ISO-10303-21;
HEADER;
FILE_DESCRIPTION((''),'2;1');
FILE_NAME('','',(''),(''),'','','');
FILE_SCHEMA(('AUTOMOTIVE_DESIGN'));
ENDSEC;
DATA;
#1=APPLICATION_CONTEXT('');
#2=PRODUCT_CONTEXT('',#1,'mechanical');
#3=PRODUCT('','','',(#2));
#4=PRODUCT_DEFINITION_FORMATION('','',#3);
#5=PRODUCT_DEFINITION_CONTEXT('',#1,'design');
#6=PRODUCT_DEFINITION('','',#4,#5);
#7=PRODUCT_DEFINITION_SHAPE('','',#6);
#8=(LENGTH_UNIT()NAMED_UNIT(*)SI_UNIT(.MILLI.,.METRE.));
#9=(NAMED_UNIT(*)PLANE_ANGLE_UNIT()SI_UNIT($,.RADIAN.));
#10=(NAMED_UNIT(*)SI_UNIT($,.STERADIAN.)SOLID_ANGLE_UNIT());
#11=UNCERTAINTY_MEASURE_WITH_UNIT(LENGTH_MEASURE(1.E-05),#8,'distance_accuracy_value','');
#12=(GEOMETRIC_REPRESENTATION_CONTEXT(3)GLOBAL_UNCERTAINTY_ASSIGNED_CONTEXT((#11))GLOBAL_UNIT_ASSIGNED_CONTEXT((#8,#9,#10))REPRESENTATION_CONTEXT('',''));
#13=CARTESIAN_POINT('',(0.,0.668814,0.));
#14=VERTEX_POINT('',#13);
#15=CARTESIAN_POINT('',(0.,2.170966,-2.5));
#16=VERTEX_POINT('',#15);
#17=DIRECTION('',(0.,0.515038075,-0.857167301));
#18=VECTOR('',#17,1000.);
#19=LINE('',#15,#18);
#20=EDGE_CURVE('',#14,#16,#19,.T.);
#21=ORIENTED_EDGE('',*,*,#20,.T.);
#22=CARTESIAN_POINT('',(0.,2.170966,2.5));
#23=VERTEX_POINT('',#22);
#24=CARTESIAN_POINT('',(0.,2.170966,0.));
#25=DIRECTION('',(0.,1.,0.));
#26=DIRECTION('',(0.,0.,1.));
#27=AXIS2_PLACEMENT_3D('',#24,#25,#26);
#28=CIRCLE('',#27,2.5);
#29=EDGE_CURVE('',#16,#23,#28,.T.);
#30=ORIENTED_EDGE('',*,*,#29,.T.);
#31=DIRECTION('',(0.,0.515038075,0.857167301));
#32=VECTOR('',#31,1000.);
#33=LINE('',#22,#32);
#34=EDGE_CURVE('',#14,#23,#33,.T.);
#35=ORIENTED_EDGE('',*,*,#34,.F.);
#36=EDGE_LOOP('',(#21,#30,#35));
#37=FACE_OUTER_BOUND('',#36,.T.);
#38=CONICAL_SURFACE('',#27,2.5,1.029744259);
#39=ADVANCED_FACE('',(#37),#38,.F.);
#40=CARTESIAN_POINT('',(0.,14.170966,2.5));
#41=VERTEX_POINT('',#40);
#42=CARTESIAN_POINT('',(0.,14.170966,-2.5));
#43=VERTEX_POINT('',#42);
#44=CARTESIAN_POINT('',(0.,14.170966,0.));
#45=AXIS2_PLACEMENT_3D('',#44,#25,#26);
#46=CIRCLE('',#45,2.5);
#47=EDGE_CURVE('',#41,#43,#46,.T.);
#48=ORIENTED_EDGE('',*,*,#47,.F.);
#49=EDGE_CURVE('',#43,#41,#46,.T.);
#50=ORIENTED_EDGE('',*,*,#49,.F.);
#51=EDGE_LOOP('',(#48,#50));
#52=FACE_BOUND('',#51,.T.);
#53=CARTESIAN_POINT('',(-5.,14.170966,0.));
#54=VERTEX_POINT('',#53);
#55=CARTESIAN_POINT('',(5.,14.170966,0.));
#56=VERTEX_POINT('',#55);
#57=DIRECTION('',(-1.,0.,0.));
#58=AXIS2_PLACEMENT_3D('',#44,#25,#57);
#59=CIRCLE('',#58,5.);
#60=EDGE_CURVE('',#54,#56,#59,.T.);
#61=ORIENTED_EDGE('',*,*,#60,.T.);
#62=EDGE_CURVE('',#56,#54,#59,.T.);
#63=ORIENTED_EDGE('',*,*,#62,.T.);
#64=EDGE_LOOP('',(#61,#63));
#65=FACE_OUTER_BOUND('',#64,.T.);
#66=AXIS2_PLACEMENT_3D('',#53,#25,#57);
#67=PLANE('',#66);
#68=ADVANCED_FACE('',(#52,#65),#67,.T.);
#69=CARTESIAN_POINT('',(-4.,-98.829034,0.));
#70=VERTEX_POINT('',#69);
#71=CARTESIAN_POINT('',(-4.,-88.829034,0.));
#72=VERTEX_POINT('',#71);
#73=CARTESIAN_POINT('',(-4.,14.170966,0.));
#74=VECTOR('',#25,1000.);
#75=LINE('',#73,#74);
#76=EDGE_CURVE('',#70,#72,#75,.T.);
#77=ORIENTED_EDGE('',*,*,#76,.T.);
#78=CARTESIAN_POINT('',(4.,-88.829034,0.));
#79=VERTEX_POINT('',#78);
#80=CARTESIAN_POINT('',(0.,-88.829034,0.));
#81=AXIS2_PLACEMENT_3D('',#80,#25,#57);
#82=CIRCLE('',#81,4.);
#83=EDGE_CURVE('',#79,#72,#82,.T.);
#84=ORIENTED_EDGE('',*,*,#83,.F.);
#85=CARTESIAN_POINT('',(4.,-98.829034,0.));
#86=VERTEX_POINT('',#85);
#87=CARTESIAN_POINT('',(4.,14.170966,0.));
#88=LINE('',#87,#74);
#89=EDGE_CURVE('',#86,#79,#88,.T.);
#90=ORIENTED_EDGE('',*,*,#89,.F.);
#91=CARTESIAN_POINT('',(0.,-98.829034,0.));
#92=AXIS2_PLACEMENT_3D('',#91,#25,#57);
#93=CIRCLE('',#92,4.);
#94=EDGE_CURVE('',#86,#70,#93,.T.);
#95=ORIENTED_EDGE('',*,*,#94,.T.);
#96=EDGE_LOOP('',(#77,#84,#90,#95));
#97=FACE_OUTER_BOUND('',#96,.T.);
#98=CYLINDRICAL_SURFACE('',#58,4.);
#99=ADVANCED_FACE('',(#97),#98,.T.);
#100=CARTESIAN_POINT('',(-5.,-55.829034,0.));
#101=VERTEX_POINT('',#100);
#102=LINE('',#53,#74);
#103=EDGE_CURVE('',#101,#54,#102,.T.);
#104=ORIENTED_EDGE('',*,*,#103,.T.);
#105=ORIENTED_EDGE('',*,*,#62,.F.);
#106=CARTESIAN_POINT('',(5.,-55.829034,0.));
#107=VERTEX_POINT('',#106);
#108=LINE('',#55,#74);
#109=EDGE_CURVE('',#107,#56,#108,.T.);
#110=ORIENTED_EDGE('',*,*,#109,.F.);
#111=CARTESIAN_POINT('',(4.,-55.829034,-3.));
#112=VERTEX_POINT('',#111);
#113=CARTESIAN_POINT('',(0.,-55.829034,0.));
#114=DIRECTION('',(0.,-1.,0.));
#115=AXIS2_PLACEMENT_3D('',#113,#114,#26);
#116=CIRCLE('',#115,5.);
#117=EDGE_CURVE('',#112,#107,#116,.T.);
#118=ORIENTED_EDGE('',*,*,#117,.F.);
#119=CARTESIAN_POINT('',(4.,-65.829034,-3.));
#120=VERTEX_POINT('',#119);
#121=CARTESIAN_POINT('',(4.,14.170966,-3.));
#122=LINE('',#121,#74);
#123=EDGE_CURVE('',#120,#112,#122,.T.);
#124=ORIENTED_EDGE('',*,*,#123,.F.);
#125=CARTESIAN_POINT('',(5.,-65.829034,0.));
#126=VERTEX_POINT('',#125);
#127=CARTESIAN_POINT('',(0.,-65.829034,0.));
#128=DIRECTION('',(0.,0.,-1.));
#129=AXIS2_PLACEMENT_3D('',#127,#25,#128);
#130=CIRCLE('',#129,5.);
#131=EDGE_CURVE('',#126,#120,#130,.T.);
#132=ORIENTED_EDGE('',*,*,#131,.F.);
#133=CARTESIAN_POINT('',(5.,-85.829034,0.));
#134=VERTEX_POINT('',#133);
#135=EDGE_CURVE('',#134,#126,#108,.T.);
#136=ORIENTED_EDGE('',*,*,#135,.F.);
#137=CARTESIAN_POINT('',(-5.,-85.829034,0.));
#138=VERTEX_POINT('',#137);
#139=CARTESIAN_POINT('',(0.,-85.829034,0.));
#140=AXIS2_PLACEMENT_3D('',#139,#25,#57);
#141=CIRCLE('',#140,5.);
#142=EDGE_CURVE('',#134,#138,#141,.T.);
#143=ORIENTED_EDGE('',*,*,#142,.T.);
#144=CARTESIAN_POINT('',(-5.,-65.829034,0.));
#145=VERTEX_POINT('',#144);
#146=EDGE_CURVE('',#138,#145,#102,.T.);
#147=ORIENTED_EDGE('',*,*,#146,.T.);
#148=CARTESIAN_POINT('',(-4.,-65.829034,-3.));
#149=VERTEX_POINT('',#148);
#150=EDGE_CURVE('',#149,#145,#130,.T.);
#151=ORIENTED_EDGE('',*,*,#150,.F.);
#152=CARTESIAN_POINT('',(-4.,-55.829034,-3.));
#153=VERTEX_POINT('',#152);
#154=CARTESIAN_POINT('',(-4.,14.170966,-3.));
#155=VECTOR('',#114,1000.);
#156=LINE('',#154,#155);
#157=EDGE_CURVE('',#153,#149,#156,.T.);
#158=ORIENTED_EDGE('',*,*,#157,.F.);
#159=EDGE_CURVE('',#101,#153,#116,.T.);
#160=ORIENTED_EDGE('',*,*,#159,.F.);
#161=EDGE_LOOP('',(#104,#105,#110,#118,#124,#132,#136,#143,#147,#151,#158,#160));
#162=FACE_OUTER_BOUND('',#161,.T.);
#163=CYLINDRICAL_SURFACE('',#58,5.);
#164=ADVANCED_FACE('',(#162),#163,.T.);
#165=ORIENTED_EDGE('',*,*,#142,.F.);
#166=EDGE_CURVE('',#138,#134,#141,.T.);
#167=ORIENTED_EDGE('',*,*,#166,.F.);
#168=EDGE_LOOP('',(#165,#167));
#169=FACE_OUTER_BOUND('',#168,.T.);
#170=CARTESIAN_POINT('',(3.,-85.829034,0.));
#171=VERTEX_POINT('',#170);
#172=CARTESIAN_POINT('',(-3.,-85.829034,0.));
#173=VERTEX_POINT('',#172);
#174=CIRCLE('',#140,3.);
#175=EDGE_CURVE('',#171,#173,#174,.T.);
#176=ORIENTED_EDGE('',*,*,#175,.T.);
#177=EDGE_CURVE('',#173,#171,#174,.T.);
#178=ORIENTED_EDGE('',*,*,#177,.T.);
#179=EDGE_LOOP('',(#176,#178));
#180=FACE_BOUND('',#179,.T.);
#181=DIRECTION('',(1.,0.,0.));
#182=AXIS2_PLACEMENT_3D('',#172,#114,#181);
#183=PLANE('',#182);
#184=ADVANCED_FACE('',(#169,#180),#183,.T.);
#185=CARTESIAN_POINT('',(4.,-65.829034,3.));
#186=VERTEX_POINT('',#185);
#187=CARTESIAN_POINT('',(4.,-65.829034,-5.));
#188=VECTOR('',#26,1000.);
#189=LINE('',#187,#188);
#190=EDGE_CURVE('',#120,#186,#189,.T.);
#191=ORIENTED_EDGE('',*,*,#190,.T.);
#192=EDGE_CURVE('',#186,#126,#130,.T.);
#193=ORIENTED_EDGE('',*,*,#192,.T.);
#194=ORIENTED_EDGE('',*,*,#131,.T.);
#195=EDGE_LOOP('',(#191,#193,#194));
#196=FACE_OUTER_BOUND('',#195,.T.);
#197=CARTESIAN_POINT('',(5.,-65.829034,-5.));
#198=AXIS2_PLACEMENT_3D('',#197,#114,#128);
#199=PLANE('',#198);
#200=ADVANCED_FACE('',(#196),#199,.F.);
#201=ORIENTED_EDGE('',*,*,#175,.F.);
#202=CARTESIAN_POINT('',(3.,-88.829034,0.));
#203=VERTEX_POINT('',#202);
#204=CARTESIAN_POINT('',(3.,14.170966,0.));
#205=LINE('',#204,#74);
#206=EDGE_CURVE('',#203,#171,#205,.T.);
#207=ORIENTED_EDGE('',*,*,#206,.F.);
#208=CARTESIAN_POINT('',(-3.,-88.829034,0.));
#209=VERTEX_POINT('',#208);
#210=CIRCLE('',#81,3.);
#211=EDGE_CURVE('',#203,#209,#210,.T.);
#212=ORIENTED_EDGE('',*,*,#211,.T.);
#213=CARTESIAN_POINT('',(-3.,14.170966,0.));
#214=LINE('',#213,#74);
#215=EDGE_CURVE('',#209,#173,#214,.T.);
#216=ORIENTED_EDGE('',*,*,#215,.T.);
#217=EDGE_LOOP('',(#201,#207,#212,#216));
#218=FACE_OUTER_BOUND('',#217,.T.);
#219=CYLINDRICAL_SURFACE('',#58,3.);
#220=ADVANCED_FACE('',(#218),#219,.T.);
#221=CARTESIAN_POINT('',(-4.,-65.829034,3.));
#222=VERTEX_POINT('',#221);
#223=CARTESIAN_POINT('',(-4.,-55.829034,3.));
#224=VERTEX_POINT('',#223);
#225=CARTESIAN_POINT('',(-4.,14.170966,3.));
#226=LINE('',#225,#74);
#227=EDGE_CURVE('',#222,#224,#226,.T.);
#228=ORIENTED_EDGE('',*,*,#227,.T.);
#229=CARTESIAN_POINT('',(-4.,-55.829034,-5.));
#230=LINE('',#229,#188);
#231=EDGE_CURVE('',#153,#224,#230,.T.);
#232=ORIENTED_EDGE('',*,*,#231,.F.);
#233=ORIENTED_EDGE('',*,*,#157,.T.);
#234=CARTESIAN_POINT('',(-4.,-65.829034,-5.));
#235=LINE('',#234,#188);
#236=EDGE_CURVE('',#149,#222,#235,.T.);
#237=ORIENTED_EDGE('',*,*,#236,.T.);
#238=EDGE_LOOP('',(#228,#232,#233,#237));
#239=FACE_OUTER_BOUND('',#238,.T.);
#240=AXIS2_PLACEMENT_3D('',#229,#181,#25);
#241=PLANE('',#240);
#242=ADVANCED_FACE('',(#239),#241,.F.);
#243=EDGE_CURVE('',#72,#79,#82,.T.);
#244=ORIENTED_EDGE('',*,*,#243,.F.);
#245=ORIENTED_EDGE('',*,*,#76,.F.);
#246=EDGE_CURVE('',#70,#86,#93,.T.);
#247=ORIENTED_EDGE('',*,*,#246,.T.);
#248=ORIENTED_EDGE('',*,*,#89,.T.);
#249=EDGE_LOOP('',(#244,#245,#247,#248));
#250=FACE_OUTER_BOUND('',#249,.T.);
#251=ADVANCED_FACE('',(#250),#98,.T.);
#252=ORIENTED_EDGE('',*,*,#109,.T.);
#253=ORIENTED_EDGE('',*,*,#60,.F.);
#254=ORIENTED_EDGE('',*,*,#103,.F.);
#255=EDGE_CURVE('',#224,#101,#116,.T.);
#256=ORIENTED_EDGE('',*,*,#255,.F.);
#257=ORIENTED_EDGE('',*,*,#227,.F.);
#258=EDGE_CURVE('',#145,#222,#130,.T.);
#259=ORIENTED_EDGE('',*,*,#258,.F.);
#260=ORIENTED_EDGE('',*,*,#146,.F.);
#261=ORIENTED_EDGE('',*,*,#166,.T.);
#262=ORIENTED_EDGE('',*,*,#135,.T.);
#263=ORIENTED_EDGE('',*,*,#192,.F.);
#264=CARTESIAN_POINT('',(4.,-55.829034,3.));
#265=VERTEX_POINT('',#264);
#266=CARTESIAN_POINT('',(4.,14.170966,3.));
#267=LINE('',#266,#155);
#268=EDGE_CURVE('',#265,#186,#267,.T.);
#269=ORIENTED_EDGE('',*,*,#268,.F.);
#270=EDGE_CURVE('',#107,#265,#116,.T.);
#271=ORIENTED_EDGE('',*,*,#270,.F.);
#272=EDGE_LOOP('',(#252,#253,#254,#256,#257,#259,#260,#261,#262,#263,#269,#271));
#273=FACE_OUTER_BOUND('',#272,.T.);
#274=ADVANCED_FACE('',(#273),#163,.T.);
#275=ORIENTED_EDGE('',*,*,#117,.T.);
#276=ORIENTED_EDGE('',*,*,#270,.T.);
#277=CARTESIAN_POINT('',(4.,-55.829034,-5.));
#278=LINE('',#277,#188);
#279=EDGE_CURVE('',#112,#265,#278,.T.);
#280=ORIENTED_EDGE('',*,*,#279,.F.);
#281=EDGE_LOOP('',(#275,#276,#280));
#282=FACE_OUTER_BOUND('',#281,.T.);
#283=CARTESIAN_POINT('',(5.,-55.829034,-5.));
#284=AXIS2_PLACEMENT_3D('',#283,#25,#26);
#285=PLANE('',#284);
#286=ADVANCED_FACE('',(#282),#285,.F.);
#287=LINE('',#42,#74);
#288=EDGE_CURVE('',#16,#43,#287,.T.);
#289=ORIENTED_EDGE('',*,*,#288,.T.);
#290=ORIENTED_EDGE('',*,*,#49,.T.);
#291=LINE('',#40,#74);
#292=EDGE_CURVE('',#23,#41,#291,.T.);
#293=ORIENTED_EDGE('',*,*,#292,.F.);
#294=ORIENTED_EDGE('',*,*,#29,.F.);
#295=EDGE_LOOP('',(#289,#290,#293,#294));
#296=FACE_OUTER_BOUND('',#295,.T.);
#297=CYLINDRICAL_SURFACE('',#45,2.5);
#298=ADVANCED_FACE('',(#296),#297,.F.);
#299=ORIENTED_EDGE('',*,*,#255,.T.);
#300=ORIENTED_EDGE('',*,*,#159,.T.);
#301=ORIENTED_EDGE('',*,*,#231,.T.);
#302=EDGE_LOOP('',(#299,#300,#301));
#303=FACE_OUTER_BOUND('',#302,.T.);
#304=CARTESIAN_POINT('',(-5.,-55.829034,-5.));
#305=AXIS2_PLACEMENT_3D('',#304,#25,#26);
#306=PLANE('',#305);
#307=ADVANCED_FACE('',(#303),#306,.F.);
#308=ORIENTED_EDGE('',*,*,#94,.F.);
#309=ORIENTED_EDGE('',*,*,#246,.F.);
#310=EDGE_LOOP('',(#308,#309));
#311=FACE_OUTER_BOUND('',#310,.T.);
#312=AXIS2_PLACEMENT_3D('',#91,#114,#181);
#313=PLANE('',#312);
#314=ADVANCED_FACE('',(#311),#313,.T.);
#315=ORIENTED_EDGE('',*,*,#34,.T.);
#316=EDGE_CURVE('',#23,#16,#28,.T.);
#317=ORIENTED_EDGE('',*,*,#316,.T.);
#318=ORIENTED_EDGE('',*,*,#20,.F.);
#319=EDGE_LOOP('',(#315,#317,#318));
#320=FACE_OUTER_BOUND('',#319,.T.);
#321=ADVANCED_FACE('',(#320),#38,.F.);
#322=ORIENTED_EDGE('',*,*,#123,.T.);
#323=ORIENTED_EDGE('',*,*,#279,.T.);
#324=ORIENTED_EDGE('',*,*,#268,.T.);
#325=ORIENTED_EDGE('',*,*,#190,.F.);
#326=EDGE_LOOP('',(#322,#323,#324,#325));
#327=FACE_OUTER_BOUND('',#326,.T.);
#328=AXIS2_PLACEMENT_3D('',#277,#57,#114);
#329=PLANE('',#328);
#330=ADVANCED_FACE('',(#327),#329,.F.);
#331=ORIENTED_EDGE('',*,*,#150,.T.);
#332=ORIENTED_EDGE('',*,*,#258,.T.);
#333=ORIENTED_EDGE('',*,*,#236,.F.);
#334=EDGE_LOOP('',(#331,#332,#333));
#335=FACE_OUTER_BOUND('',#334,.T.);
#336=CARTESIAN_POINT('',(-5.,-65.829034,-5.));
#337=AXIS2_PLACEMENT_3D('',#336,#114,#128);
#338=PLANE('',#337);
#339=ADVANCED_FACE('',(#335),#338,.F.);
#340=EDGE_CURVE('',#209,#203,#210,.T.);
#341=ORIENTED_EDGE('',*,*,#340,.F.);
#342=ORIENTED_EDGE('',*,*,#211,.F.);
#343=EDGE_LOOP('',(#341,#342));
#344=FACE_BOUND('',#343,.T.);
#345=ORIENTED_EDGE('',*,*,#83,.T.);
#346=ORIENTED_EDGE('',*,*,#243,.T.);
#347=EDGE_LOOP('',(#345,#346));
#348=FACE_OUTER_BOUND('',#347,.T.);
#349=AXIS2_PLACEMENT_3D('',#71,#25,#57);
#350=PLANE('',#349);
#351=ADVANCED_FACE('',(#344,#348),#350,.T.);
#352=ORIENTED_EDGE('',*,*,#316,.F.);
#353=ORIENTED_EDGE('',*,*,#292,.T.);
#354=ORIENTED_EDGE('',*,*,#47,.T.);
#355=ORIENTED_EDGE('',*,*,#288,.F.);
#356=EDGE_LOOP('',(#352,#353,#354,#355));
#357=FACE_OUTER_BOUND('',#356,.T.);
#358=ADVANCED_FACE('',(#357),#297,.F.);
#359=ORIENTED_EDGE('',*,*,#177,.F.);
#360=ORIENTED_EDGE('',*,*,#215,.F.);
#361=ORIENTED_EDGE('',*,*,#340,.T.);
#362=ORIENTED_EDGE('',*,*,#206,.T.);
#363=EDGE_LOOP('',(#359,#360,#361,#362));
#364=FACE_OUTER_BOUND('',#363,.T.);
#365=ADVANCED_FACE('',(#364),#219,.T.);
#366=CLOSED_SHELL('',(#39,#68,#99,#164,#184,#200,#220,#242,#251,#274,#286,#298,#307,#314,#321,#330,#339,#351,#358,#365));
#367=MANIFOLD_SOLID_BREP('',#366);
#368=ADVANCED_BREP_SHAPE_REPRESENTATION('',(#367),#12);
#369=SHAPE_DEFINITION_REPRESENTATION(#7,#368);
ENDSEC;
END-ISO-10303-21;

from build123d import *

# Parameters (mm, degrees)
CUT_EXTRUDE1_DEPTH      = 100.081673268
CUT_EXTRUDE1_DEPTH_BACK = 100.081673268
SKETCH2_W               = 1
SKETCH2_H               = 10
M6_TAPPED_HOLE1_D       = 5
M6_TAPPED_HOLE1_DEPTH   = 12
M6_TAPPED_HOLE1_TIP     = 1.502151548


with BuildPart() as part:
    # Sketch1 → Revolve1 (revolve)
    with BuildSketch(Plane.XY):
        Polygon((0, 14.170965918), (0, -98.829034082), (-4, -98.829034082), (-4, -88.829034082), (-3, -88.829034082), (-3, -85.829034082), (-5, -85.829034082), (-5, 14.170965918), align=None)
    revolve(axis=Axis((0, 14.170965918, 0), (0, -1, 0)))

    # Sketch2 → Cut-Extrude1 (cut, two sides: drawn at the far end of the back side and taken through both)
    with BuildSketch(Plane.XY.offset(-CUT_EXTRUDE1_DEPTH_BACK)):
        with Locations((-4.5, -60.829034082)):
            Rectangle(SKETCH2_W, SKETCH2_H)
        with Locations((4.5, -60.829034082)):
            Rectangle(SKETCH2_W, SKETCH2_H)
    extrude(amount=CUT_EXTRUDE1_DEPTH + CUT_EXTRUDE1_DEPTH_BACK, mode=Mode.SUBTRACT)

    # M6 Tapped Hole1
    with Locations(Plane(origin=(0, 14.170965918, 0), x_dir=(1, 0, 0), z_dir=(0, 1, 0))):
        with Locations((0, 0)):
            Hole(M6_TAPPED_HOLE1_D / 2, depth=M6_TAPPED_HOLE1_DEPTH)
            with Locations((0, 0, -(M6_TAPPED_HOLE1_DEPTH + M6_TAPPED_HOLE1_TIP / 2))):  # 118° drill point
                Cone(0, M6_TAPPED_HOLE1_D / 2, M6_TAPPED_HOLE1_TIP, mode=Mode.SUBTRACT)


solid = part.part
